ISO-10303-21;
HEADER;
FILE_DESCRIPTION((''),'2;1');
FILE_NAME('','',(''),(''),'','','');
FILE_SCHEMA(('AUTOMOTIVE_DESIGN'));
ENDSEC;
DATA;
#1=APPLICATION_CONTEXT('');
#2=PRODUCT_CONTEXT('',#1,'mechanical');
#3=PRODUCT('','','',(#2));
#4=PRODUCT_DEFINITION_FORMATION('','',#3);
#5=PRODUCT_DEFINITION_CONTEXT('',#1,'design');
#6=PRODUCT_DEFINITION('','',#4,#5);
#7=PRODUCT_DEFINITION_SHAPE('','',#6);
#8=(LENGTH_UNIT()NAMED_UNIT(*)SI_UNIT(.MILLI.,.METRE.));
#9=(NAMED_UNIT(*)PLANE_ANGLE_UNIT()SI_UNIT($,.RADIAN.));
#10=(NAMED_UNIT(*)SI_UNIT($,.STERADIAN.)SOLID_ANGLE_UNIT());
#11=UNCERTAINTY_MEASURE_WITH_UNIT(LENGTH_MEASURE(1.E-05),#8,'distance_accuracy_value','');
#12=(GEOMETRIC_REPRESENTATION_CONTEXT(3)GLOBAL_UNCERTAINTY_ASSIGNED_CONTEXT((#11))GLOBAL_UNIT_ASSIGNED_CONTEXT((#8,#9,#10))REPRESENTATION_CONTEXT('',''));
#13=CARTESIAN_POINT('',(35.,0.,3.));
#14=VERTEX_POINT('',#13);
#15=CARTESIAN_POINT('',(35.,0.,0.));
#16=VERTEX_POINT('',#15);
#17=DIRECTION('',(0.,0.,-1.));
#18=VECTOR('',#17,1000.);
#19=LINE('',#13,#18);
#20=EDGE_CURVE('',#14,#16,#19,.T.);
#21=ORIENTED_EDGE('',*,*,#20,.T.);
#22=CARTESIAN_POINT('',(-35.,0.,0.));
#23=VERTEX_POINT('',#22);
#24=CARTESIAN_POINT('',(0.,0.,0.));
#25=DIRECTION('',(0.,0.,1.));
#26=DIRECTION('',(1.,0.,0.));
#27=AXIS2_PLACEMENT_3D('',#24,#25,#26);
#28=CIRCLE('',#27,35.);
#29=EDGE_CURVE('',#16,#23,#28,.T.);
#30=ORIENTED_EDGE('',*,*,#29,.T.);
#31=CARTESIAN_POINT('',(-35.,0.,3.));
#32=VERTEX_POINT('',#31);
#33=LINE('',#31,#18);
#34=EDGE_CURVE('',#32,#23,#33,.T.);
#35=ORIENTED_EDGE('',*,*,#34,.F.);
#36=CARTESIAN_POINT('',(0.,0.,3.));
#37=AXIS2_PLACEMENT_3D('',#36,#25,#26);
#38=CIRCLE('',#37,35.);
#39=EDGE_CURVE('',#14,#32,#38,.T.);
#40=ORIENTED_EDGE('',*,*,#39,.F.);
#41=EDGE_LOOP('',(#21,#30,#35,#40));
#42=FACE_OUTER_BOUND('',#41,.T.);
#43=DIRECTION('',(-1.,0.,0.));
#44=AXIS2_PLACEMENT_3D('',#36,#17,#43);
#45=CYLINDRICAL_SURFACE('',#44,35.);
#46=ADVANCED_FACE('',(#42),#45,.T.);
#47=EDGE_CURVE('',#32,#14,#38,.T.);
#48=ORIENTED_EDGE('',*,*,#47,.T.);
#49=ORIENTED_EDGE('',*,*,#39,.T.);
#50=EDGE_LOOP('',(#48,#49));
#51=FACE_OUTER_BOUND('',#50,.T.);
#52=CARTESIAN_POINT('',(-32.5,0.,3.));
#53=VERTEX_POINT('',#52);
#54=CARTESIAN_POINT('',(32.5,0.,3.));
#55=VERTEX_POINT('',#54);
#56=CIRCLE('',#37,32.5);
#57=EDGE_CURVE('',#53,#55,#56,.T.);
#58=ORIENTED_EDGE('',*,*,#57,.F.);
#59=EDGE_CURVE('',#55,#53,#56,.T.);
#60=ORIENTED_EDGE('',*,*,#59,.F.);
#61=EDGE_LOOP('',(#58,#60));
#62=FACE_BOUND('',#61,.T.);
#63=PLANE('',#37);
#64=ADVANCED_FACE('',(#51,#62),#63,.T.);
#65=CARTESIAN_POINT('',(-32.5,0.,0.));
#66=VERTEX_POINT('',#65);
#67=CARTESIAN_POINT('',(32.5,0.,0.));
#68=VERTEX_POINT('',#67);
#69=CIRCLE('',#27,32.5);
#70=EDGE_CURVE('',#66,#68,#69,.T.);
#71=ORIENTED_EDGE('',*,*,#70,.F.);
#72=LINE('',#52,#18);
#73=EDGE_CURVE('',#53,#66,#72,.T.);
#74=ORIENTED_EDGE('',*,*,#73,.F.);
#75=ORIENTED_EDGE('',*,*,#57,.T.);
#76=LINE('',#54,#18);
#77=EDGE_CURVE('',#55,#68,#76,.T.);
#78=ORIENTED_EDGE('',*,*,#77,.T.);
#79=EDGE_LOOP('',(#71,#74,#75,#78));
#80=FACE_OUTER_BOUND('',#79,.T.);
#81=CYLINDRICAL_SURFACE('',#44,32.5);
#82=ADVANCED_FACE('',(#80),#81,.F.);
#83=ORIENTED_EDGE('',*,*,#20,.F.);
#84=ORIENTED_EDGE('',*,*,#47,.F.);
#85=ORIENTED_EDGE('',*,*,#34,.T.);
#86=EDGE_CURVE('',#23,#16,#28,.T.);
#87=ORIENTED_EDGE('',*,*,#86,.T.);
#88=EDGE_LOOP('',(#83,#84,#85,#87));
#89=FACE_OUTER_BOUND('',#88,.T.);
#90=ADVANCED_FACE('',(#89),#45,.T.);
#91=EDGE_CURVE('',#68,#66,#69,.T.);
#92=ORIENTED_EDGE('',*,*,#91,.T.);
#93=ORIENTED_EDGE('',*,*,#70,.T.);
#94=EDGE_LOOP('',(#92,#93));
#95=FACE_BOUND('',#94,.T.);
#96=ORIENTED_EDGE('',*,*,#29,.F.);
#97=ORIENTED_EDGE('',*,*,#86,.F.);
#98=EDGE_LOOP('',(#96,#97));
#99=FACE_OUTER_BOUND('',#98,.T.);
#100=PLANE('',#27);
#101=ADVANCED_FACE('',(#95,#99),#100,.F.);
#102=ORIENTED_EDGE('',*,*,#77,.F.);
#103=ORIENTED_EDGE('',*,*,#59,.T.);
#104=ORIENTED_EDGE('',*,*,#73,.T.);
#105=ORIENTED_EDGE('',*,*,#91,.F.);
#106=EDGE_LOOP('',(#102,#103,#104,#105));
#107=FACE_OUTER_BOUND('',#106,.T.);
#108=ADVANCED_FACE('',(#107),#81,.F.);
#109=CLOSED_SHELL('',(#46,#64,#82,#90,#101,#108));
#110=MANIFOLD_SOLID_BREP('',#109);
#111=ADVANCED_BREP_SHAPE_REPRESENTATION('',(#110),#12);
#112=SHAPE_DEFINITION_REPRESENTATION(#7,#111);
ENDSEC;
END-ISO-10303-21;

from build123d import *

# Parameters (mm, degrees)
SKETCH_1_R      = 35
SKETCH_1_R_2    = 32.5
EXTRUDE_1_DEPTH = 3


with BuildPart() as part:
    # 草图1 → 凸台-拉伸1 (new body)
    with BuildSketch(Plane.XY):
        Circle(SKETCH_1_R)
        Circle(SKETCH_1_R_2, mode=Mode.SUBTRACT)
    extrude(amount=EXTRUDE_1_DEPTH)


solid = part.part
